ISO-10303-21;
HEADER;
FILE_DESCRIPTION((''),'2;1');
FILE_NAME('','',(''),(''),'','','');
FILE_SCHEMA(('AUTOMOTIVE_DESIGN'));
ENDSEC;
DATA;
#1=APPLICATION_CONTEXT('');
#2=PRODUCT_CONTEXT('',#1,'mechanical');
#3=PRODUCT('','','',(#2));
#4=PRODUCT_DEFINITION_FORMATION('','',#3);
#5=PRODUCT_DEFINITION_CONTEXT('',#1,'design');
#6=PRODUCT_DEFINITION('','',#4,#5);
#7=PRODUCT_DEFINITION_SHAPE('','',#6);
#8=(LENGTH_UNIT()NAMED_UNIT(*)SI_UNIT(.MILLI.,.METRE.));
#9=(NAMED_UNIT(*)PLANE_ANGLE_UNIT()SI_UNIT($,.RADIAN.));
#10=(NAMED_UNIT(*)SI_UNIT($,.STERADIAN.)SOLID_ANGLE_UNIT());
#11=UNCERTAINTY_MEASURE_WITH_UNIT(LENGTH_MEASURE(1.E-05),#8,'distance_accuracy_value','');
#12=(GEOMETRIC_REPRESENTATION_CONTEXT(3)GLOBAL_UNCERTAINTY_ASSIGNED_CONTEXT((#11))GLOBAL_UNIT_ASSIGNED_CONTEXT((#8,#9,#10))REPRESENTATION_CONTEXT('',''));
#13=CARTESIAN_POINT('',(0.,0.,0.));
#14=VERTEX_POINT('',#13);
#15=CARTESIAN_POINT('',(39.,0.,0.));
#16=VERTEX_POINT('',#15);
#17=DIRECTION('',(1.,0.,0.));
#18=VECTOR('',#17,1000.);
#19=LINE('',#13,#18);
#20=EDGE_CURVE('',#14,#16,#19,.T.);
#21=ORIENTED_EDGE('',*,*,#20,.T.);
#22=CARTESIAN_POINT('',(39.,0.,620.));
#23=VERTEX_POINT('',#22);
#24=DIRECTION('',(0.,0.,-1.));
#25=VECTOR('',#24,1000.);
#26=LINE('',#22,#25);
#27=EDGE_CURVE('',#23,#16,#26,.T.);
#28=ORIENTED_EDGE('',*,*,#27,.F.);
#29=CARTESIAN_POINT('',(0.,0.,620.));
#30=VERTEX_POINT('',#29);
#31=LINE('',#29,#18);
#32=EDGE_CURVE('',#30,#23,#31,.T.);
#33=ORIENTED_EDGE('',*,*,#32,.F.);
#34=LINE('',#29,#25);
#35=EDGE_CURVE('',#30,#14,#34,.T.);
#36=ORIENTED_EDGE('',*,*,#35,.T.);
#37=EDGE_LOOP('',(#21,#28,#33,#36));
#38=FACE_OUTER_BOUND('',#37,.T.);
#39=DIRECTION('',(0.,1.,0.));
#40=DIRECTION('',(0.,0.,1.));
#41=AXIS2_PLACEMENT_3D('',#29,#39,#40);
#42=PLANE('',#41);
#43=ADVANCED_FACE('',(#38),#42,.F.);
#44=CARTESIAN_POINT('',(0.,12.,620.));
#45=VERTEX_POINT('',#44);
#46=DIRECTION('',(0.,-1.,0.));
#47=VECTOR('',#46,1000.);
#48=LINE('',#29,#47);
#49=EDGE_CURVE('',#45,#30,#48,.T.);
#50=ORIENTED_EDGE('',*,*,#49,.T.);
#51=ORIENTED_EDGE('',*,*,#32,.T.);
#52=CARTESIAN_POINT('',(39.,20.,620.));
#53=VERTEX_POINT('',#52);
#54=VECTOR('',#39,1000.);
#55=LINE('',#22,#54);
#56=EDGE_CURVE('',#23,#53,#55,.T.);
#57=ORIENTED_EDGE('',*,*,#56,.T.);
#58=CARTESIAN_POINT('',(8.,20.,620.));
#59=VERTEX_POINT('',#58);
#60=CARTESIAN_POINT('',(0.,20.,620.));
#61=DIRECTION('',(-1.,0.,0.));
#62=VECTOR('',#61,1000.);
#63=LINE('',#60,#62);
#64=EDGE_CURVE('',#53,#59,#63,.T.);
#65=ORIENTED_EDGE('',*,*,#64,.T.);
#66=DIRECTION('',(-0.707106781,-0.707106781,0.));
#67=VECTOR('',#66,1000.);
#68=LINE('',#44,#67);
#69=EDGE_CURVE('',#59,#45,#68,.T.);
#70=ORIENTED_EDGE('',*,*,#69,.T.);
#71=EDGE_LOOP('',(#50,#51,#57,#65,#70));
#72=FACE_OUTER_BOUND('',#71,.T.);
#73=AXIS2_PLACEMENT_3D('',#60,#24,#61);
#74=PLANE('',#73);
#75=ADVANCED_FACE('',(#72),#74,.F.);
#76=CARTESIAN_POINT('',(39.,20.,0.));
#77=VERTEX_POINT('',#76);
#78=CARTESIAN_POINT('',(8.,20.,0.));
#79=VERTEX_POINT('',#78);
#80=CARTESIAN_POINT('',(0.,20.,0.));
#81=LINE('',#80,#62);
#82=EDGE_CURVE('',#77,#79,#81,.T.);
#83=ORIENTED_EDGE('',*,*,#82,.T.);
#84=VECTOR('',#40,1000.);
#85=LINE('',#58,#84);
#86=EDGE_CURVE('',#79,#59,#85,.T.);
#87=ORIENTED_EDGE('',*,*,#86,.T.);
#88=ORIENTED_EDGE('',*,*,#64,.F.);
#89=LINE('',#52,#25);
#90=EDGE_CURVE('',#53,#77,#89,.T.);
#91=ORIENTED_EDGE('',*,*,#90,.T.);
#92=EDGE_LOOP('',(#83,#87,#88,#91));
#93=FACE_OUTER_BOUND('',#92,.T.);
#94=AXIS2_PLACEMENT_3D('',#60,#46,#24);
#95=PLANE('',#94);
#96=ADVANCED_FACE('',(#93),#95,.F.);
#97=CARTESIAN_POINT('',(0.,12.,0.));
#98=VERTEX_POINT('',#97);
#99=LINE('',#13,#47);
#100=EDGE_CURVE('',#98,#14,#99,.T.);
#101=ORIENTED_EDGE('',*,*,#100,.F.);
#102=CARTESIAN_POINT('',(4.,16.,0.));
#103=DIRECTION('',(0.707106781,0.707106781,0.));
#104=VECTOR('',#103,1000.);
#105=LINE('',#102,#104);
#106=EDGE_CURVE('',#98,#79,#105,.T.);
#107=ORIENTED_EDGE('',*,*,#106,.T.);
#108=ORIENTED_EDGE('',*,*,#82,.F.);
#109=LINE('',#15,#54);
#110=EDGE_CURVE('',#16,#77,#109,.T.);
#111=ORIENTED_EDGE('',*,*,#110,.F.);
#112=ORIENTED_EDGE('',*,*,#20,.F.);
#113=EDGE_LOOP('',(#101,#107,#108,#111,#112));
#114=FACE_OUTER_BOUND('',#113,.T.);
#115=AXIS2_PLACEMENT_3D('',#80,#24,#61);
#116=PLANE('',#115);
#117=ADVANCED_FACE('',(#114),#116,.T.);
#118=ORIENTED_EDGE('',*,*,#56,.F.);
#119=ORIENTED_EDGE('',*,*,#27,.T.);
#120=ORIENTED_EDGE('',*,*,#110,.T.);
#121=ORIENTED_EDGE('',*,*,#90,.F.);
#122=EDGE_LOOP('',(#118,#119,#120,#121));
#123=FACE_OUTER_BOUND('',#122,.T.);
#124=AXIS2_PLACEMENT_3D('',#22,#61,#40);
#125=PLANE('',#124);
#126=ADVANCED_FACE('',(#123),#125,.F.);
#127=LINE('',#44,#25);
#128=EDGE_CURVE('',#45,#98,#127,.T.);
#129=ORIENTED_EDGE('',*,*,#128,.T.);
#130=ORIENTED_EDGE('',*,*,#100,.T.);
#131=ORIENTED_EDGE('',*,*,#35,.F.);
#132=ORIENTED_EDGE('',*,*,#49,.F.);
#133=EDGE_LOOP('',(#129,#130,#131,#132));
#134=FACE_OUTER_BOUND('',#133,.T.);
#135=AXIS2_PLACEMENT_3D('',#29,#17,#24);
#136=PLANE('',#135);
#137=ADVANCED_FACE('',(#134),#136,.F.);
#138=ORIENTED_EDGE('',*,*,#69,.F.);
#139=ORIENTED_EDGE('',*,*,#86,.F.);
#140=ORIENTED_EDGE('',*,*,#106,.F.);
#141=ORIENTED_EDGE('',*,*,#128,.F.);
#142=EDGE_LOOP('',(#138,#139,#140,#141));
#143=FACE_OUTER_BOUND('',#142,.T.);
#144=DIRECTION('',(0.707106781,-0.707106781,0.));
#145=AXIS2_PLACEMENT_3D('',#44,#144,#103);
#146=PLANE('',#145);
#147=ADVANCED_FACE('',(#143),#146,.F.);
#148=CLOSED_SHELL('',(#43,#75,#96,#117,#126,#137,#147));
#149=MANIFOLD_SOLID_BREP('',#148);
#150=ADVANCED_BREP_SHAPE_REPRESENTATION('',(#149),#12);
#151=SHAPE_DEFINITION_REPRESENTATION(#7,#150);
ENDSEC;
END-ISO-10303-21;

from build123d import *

# Parameters (mm, degrees)
SKETCH1_W           = 39
SKETCH1_H           = 20
BOSS_EXTRUDE1_DEPTH = 620
CHAMFER1_SIZE       = 8


with BuildPart() as part:
    # Sketch1 → Boss-Extrude1 (new body)
    with BuildSketch(Plane.XY):
        with Locations((19.5, 10)):
            Rectangle(SKETCH1_W, SKETCH1_H)
    extrude(amount=BOSS_EXTRUDE1_DEPTH)

    # Chamfer1
    chamfer1_edges = [part.edges().sort_by_distance(p)[0] for p in [
        (0, 20, 310),
    ]]
    chamfer(chamfer1_edges, length=CHAMFER1_SIZE)


solid = part.part
